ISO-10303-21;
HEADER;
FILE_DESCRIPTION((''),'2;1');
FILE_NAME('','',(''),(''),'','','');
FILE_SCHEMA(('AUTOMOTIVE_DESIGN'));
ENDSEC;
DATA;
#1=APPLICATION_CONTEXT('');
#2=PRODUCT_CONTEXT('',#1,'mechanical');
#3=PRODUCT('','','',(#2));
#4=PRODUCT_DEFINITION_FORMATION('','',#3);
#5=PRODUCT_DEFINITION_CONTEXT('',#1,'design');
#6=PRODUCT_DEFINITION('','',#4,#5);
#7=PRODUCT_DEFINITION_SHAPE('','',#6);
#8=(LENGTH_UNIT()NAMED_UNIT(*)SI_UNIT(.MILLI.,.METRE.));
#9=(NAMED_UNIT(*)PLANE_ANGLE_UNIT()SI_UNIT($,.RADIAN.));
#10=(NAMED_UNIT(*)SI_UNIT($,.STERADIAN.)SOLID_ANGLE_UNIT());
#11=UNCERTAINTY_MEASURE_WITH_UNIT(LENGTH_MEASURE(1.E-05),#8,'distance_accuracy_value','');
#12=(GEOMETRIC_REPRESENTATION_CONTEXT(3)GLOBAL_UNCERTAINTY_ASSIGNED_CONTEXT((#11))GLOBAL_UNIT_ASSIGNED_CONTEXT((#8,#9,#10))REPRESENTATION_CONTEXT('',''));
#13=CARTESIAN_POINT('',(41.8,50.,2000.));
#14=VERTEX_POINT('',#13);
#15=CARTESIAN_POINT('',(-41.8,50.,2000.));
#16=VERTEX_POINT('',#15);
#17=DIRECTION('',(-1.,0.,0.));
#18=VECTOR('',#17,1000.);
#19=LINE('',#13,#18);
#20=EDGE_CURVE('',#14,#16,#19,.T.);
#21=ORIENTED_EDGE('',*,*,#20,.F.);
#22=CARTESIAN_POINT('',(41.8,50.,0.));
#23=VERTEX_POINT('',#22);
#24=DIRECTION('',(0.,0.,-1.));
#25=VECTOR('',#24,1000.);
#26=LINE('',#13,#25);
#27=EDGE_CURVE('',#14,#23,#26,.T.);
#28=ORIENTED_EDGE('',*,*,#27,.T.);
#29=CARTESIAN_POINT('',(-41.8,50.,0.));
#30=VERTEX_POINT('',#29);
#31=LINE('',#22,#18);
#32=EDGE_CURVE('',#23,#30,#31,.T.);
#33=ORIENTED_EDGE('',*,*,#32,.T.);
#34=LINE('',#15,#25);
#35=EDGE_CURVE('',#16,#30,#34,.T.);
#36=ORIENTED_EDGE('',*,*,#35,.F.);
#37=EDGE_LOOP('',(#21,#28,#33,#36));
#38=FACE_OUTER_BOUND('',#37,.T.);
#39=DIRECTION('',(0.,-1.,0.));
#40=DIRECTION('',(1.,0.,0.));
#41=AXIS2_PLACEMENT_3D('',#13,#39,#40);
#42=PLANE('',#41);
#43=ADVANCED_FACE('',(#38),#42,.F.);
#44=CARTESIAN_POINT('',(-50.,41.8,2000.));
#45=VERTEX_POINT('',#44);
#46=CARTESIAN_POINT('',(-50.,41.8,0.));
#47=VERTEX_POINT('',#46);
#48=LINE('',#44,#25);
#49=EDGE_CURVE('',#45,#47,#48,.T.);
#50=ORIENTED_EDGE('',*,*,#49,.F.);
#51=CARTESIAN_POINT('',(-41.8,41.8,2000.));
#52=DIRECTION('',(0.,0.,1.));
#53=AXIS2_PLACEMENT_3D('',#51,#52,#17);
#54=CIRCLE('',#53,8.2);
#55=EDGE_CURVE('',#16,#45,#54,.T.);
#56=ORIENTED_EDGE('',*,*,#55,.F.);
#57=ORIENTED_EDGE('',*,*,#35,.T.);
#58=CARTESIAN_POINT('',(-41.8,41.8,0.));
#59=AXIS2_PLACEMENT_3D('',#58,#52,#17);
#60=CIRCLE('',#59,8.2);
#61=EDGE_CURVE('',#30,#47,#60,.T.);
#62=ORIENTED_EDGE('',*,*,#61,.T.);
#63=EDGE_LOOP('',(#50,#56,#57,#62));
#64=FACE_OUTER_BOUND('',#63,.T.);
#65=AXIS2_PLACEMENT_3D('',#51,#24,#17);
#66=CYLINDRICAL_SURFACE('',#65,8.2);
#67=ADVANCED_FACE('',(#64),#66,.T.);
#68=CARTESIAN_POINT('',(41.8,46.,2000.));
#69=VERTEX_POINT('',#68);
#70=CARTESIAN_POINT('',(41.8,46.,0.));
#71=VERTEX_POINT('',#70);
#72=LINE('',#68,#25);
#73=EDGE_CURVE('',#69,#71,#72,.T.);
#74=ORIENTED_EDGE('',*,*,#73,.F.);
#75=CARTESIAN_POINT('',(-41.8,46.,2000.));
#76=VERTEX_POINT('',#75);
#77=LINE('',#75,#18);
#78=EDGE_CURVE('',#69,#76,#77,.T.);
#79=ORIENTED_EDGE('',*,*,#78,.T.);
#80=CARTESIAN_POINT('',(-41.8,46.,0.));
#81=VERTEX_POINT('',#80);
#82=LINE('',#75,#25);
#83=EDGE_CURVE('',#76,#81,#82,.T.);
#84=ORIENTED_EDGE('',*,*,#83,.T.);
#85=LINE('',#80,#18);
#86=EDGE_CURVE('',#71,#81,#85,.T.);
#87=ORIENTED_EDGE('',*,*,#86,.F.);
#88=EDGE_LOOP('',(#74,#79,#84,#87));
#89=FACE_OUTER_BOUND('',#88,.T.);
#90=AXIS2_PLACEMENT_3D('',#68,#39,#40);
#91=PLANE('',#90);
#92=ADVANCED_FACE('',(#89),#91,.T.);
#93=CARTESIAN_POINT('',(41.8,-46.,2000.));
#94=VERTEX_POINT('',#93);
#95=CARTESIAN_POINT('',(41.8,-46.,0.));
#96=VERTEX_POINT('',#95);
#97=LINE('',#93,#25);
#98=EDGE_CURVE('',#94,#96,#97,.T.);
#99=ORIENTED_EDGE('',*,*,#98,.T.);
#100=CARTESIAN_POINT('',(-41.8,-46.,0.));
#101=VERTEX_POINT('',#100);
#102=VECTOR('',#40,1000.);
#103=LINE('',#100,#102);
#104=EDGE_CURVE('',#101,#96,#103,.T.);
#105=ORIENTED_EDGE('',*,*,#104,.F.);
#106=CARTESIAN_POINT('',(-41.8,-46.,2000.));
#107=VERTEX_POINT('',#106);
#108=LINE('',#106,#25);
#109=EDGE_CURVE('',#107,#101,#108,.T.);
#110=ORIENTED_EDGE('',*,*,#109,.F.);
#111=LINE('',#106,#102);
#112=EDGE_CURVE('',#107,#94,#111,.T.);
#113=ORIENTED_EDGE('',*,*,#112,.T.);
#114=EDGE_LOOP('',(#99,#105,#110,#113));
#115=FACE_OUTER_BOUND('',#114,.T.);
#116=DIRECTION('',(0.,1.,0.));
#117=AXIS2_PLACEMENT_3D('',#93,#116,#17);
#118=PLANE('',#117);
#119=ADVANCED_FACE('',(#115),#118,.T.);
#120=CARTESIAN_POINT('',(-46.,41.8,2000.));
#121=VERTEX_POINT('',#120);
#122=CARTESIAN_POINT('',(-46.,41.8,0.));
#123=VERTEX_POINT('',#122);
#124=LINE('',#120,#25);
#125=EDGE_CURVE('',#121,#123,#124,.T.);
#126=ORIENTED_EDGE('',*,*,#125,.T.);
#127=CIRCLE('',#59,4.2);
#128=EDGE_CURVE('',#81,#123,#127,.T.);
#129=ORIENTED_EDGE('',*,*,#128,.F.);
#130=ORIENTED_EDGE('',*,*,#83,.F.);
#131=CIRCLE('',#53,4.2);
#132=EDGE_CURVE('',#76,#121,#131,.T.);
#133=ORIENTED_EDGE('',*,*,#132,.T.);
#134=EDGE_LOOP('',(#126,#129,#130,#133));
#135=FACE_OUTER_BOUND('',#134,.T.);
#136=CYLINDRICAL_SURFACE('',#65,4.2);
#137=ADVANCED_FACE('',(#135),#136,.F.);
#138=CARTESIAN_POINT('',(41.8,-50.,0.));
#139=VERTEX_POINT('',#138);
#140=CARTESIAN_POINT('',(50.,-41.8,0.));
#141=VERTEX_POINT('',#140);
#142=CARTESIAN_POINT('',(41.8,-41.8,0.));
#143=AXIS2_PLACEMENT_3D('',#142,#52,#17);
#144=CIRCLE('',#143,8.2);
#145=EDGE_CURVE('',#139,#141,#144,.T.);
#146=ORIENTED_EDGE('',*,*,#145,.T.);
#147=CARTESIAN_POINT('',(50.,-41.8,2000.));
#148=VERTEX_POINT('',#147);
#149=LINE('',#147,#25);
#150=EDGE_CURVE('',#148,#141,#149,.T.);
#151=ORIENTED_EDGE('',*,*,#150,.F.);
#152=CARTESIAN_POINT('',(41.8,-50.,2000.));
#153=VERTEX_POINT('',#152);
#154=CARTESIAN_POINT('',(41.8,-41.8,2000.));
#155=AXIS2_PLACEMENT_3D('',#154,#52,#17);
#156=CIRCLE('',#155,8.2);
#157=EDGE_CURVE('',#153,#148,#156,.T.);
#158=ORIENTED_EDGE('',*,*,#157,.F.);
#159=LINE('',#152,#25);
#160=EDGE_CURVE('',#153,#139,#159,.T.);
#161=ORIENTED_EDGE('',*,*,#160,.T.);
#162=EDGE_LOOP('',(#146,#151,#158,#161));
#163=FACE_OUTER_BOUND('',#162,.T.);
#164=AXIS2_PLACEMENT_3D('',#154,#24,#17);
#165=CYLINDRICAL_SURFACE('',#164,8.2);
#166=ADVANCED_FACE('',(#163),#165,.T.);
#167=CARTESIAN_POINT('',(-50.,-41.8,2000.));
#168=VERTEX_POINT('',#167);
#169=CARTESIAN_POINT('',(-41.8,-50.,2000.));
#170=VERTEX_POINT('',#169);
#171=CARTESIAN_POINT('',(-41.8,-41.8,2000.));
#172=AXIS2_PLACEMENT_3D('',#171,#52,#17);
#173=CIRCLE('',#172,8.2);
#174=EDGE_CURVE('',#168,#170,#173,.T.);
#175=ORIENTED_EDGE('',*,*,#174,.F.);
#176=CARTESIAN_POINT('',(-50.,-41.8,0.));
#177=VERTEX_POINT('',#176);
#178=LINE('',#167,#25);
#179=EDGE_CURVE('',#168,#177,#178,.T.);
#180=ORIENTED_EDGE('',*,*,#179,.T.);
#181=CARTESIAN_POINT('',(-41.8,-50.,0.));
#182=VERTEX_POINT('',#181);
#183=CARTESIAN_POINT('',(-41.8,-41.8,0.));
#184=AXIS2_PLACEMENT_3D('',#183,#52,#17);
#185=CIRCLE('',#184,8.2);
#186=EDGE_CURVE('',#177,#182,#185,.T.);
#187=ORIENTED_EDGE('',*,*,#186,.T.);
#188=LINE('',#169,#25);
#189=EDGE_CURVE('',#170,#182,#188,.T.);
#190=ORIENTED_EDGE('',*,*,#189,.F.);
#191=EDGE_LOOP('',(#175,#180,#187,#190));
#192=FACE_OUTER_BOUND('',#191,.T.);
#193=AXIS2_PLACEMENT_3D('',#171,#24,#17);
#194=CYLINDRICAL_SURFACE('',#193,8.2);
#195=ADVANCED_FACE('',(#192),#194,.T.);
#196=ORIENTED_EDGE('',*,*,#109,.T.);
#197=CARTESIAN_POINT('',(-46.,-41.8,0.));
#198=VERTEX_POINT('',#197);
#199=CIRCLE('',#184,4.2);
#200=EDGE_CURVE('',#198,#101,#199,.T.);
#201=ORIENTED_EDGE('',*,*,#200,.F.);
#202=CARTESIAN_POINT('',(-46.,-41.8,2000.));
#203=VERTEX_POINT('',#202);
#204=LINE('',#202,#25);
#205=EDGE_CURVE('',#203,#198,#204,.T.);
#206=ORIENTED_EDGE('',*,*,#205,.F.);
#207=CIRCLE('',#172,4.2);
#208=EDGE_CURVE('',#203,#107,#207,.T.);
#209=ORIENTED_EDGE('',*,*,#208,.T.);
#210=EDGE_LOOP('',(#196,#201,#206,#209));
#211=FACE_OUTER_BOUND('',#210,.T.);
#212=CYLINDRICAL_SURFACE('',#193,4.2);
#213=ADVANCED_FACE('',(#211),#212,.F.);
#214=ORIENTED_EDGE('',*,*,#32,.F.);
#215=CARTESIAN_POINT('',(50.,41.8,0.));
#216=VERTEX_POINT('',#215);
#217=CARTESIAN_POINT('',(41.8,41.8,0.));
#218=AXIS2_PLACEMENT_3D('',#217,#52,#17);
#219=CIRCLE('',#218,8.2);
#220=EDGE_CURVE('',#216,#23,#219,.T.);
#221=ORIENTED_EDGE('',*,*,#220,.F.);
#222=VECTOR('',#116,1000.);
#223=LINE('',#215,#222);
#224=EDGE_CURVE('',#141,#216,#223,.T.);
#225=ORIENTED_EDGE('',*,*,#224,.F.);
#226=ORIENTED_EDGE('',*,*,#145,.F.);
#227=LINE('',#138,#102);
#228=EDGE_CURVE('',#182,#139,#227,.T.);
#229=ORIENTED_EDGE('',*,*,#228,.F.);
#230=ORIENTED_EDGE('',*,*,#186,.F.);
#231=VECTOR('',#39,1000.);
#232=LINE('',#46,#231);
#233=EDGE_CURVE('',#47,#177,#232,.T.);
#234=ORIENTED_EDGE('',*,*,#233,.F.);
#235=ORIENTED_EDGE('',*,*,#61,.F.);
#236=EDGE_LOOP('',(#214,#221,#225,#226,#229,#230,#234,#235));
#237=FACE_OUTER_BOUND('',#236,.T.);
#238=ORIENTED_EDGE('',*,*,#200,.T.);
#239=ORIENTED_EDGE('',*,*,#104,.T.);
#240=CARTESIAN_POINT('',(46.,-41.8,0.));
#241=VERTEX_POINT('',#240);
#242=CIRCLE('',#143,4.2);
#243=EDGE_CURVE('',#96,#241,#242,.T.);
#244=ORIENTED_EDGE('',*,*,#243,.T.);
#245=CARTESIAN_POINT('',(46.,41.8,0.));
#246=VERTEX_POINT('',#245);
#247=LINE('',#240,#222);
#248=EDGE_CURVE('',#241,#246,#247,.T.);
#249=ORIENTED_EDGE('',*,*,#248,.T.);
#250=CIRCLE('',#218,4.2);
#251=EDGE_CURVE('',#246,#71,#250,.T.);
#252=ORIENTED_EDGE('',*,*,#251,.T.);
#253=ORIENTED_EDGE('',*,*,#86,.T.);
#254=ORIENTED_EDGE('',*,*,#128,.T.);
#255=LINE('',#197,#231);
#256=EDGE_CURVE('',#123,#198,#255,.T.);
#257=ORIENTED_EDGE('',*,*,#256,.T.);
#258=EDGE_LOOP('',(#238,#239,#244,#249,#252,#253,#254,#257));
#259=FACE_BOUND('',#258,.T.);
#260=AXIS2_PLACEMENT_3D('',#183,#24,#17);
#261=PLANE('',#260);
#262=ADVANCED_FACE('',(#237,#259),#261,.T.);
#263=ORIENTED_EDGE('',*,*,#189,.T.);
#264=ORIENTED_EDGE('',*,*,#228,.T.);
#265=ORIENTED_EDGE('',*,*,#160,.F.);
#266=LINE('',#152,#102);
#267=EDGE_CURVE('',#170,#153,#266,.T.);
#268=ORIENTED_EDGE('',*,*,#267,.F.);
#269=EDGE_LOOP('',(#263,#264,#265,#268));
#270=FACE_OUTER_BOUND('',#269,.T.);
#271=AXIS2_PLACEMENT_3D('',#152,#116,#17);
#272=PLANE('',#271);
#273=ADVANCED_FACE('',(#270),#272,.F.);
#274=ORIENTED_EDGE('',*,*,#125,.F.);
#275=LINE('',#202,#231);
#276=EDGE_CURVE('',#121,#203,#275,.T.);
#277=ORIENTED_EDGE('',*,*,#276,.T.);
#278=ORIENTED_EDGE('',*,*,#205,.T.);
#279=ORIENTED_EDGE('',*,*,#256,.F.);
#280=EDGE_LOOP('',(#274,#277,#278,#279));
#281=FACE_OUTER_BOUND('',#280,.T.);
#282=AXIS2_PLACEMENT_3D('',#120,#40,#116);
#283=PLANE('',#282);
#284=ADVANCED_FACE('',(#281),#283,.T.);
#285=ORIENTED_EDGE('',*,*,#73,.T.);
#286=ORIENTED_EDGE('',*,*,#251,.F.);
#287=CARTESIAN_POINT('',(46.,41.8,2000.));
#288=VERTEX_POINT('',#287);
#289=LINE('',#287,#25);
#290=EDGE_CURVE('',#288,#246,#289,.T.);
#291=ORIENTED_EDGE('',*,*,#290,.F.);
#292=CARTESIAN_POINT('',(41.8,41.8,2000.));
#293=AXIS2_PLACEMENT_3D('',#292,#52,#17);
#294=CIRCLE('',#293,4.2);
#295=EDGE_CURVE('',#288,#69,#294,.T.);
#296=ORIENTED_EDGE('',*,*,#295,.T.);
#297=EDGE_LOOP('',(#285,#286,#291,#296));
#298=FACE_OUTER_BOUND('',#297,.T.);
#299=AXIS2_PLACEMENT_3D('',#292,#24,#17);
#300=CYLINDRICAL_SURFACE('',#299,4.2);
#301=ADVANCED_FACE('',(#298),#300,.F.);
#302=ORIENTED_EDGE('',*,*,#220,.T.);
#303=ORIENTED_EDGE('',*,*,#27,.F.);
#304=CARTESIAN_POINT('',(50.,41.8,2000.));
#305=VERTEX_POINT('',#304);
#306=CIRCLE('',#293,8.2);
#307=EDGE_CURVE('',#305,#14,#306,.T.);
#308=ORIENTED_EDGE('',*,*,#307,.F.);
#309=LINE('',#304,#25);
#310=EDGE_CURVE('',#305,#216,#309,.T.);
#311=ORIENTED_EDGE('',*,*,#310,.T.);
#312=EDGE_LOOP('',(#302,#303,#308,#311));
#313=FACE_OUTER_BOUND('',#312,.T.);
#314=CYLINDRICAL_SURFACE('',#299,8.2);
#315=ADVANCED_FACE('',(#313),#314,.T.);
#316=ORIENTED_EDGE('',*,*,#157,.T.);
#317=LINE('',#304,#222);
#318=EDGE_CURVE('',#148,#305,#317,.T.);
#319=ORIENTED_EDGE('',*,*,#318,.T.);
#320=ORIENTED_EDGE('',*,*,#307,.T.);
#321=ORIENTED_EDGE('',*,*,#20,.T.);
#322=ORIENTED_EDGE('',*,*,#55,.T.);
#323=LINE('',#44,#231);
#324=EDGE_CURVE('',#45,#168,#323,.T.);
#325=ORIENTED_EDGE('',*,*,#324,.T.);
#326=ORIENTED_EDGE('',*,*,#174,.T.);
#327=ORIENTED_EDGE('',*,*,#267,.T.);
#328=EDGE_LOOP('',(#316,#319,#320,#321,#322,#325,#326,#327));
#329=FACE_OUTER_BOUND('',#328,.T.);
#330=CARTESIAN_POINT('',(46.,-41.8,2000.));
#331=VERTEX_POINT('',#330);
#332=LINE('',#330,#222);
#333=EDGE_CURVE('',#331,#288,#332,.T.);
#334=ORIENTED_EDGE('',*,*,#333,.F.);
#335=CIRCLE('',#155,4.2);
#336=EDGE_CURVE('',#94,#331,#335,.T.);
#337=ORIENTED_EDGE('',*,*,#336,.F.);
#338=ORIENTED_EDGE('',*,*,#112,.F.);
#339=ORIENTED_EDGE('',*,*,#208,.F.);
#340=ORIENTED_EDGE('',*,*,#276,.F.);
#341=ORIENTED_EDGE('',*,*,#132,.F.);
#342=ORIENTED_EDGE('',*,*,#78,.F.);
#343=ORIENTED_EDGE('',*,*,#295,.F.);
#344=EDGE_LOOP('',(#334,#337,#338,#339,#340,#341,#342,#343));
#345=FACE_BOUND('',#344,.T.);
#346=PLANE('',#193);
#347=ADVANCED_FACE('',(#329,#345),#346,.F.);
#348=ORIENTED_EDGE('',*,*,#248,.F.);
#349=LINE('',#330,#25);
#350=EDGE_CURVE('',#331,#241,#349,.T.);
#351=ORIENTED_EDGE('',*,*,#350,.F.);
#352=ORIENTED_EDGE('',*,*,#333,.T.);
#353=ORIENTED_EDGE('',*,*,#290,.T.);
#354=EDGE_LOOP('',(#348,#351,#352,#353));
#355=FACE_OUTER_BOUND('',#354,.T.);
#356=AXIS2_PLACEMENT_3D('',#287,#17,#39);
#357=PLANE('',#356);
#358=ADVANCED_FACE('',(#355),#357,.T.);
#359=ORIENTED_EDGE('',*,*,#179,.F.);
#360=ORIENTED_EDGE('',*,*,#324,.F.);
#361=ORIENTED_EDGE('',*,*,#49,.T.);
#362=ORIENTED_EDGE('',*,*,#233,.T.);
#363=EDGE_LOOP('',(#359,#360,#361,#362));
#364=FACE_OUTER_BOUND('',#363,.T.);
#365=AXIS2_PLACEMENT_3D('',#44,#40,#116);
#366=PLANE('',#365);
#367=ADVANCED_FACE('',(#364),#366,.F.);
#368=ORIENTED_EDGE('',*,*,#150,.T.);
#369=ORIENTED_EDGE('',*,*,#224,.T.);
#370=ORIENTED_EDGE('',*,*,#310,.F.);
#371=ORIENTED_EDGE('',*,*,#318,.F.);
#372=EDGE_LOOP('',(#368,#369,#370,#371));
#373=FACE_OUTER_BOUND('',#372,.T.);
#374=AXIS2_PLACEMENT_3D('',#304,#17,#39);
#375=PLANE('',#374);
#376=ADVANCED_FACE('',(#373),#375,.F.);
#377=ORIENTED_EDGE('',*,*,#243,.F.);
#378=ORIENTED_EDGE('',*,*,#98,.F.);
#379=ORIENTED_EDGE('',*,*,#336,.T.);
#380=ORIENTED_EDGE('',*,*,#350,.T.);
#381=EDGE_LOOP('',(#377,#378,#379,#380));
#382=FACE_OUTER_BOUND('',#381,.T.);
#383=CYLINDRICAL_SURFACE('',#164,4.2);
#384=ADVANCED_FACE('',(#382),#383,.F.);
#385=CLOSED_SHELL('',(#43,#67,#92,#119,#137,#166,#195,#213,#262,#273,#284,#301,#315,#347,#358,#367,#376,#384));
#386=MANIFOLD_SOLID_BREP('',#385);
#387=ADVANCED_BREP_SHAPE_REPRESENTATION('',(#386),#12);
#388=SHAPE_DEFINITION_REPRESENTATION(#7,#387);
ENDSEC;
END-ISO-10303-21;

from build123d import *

# Parameters (mm, degrees)
BOSS_EXTRUDE1_DEPTH = 2000
SHELL1_T            = -4


with BuildPart() as part:
    # Sketch1 → Boss-Extrude1 (new body)
    with BuildSketch(Plane.XY):
        with BuildLine():
            Line((41.8, 50), (-41.8, 50))
            ThreePointArc((-41.8, 50), (-47.598275606, 47.598275606), (-50, 41.8))
            Line((-50, 41.8), (-50, -41.8))
            ThreePointArc((-50, -41.8), (-47.598275606, -47.598275606), (-41.8, -50))
            Line((-41.8, -50), (41.8, -50))
            ThreePointArc((41.8, -50), (47.598275606, -47.598275606), (50, -41.8))
            Line((50, -41.8), (50, 41.8))
            ThreePointArc((50, 41.8), (47.598275606, 47.598275606), (41.8, 50))
        make_face()
    extrude(amount=BOSS_EXTRUDE1_DEPTH)

    # Shell1
    shell1_openings = [part.faces().sort_by_distance(p)[0] for p in [
        (0, 0, 2000),
        (0, 0, 0),
    ]]
    offset(amount=SHELL1_T, openings=shell1_openings, kind=Kind.INTERSECTION)


solid = part.part
